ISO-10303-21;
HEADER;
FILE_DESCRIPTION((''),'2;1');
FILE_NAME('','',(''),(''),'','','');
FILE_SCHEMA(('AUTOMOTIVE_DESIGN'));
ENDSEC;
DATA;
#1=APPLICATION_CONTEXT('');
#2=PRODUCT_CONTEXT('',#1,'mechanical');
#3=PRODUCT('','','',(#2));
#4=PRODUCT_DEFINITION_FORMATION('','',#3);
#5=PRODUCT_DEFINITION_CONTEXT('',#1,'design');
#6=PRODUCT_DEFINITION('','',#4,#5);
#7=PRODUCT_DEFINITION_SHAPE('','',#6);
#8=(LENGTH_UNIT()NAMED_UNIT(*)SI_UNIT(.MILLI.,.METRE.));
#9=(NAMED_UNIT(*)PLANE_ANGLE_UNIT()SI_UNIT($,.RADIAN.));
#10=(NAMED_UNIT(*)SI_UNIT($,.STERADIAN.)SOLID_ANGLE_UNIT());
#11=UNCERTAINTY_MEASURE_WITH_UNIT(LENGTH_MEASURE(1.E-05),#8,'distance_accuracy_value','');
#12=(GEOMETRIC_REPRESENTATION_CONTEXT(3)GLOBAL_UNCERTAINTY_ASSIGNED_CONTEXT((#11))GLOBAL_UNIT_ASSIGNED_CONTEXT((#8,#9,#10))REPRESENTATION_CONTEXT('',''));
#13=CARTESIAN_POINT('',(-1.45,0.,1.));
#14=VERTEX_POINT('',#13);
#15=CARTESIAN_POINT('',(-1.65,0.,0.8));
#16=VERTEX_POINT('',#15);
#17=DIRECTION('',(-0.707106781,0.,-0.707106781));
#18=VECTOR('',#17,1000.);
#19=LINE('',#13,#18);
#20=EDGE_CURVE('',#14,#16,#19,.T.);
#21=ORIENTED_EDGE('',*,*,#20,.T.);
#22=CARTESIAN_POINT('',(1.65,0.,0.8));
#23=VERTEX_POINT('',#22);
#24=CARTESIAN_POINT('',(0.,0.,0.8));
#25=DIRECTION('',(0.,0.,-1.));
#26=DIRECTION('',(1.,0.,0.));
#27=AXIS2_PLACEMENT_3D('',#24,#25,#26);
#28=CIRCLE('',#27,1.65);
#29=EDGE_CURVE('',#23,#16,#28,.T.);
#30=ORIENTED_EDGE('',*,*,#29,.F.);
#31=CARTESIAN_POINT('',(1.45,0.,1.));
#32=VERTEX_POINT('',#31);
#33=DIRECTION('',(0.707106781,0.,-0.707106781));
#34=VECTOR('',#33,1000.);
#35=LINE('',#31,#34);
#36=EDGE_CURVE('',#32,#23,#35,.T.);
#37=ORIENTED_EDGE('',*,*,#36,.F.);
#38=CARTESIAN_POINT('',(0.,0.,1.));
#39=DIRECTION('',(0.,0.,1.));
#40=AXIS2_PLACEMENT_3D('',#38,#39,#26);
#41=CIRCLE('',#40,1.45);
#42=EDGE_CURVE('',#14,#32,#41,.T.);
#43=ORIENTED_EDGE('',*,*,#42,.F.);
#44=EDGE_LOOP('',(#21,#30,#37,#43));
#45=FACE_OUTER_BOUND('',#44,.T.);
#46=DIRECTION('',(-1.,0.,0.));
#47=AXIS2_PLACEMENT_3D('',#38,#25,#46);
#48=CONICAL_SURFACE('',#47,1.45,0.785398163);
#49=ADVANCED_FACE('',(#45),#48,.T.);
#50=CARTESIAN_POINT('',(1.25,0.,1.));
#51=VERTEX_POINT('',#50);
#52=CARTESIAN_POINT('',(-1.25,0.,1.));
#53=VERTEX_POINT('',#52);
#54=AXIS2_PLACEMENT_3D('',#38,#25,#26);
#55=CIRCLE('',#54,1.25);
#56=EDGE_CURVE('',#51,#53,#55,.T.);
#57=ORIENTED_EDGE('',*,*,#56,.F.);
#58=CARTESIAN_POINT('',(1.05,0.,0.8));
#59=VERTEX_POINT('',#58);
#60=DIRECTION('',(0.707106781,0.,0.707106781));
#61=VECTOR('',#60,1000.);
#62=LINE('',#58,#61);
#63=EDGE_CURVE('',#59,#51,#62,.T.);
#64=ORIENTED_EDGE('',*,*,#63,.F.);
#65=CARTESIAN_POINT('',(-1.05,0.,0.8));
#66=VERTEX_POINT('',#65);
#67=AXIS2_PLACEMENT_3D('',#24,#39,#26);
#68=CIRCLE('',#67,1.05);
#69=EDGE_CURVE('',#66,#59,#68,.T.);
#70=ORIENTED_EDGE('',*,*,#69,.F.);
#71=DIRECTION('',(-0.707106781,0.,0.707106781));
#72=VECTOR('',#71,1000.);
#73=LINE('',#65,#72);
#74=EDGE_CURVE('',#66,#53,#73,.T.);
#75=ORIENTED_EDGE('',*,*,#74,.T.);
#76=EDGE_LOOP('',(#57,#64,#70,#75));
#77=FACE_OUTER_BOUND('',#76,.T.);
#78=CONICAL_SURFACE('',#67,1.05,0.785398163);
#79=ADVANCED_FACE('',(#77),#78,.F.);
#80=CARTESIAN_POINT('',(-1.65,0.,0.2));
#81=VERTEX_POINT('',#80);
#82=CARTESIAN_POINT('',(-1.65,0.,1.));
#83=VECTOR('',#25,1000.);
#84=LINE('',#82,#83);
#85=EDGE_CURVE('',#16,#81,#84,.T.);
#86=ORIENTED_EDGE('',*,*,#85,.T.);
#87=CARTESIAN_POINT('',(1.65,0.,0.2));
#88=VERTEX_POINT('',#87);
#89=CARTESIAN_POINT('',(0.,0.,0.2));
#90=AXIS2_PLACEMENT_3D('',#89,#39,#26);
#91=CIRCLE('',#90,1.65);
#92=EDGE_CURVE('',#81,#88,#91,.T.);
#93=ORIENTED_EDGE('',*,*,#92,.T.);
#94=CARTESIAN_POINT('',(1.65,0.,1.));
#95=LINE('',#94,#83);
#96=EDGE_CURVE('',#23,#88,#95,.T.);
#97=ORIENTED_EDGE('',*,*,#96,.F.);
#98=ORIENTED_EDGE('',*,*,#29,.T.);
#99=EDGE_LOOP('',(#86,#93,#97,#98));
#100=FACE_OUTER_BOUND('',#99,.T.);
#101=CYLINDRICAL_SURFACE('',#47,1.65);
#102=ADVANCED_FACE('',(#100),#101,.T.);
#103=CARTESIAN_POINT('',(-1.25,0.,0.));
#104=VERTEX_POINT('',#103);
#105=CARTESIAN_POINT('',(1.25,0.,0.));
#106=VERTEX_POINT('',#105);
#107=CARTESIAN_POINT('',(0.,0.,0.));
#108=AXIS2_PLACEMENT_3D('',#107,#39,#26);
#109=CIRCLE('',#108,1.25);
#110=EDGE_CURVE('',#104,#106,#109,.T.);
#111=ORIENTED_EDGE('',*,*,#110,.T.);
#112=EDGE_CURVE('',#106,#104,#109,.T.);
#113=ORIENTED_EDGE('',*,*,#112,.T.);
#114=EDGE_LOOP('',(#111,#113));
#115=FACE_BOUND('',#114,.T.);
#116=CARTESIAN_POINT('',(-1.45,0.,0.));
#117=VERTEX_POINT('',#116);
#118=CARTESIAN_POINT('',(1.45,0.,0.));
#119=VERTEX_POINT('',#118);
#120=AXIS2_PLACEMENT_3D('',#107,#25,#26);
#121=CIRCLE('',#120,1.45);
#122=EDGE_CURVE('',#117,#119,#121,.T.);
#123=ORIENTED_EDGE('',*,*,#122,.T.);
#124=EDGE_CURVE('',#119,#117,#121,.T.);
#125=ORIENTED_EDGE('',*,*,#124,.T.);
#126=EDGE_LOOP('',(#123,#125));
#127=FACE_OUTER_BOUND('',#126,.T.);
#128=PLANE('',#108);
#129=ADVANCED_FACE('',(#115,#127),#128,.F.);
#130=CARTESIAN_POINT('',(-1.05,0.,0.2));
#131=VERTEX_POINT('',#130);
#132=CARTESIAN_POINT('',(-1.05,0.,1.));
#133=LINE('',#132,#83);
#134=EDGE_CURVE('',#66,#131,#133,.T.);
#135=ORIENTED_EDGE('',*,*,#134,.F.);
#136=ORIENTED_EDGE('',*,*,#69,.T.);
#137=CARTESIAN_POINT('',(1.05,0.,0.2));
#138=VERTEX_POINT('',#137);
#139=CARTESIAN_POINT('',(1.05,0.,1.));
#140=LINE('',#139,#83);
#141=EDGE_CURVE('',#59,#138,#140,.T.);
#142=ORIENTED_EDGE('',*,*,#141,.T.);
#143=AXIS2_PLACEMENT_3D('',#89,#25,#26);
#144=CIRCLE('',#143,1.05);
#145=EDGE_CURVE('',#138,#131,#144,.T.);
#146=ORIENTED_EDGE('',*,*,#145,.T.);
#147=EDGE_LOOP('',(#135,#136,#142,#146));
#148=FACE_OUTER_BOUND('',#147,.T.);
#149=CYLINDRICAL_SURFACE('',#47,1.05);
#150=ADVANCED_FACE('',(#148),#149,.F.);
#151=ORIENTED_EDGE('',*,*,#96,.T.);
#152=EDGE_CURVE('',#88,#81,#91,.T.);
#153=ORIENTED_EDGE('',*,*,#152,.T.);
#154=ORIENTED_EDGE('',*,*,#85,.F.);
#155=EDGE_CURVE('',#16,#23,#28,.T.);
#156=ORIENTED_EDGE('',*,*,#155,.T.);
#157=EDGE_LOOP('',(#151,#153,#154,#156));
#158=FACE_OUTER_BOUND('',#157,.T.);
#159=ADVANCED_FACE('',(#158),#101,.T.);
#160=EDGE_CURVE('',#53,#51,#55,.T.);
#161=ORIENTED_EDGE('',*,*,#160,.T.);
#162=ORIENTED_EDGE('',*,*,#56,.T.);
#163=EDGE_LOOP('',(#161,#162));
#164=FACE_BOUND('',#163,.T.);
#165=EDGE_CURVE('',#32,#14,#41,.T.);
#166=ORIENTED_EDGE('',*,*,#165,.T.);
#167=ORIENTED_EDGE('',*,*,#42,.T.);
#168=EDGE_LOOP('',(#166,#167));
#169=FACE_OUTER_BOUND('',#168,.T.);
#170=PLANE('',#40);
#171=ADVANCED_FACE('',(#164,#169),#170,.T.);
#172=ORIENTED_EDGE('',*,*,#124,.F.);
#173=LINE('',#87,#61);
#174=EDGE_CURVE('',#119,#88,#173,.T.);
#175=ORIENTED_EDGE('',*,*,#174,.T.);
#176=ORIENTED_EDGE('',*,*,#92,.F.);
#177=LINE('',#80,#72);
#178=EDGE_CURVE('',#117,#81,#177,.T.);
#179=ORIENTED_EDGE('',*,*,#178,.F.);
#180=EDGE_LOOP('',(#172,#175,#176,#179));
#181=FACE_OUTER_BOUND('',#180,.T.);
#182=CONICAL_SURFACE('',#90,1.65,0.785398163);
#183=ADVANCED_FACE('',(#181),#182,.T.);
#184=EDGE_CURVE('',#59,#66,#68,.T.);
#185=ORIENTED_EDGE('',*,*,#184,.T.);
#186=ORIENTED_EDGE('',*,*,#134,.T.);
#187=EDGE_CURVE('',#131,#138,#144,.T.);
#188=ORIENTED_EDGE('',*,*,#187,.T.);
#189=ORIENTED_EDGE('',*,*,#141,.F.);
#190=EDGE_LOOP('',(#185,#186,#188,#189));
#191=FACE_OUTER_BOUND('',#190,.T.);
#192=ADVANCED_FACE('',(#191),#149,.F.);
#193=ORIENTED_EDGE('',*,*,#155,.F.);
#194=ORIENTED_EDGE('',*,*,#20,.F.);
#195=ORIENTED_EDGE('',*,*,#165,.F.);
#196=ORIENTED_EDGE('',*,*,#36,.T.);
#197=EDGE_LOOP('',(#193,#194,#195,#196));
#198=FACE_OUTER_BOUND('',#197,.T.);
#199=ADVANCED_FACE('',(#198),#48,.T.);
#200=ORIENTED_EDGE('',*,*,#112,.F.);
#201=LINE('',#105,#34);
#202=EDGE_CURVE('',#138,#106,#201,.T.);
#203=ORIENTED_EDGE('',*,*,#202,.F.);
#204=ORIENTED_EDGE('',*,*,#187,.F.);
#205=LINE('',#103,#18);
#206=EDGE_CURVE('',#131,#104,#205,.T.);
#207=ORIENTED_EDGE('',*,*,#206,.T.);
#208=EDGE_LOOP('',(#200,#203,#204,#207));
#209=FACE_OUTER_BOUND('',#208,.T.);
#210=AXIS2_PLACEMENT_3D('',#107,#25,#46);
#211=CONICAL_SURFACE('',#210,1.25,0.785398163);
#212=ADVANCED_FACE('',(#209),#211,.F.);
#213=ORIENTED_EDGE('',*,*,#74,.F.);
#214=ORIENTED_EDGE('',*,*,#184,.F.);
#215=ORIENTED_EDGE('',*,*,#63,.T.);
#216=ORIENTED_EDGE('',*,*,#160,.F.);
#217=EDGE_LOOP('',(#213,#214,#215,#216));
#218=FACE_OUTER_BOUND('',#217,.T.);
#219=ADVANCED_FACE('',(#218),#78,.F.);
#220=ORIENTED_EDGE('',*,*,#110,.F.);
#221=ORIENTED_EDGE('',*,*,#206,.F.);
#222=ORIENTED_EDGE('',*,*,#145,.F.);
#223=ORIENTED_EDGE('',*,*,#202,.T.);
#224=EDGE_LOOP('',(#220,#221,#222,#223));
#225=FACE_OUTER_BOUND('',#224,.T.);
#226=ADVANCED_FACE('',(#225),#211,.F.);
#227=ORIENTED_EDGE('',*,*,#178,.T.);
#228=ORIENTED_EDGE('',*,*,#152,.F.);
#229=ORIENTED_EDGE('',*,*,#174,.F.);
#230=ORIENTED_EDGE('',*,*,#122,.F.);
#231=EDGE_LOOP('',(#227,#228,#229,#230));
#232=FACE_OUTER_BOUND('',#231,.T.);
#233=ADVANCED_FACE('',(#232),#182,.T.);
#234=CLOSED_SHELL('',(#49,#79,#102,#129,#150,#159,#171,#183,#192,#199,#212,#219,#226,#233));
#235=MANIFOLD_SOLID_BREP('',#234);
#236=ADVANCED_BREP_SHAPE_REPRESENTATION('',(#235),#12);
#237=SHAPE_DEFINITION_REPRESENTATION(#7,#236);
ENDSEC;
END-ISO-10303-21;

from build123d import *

# Parameters (mm, degrees)
SKETCH1_R           = 1.65
SKETCH1_R_2         = 1.05
BOSS_EXTRUDE1_DEPTH = 1
CHAMFER1_SIZE       = 0.2


with BuildPart() as part:
    # Sketch1 → Boss-Extrude1 (new body)
    with BuildSketch(Plane.XY):
        Circle(SKETCH1_R)
        Circle(SKETCH1_R_2, mode=Mode.SUBTRACT)
    extrude(amount=BOSS_EXTRUDE1_DEPTH)

    # Chamfer1
    chamfer1_edges = [part.edges().sort_by_distance(p)[0] for p in [
        (-1.65, 0, 0),
        (-1.65, 0, 1),
        (-1.05, 0, 0),
        (-1.05, 0, 1),
    ]]
    chamfer(chamfer1_edges, length=CHAMFER1_SIZE)


solid = part.part
